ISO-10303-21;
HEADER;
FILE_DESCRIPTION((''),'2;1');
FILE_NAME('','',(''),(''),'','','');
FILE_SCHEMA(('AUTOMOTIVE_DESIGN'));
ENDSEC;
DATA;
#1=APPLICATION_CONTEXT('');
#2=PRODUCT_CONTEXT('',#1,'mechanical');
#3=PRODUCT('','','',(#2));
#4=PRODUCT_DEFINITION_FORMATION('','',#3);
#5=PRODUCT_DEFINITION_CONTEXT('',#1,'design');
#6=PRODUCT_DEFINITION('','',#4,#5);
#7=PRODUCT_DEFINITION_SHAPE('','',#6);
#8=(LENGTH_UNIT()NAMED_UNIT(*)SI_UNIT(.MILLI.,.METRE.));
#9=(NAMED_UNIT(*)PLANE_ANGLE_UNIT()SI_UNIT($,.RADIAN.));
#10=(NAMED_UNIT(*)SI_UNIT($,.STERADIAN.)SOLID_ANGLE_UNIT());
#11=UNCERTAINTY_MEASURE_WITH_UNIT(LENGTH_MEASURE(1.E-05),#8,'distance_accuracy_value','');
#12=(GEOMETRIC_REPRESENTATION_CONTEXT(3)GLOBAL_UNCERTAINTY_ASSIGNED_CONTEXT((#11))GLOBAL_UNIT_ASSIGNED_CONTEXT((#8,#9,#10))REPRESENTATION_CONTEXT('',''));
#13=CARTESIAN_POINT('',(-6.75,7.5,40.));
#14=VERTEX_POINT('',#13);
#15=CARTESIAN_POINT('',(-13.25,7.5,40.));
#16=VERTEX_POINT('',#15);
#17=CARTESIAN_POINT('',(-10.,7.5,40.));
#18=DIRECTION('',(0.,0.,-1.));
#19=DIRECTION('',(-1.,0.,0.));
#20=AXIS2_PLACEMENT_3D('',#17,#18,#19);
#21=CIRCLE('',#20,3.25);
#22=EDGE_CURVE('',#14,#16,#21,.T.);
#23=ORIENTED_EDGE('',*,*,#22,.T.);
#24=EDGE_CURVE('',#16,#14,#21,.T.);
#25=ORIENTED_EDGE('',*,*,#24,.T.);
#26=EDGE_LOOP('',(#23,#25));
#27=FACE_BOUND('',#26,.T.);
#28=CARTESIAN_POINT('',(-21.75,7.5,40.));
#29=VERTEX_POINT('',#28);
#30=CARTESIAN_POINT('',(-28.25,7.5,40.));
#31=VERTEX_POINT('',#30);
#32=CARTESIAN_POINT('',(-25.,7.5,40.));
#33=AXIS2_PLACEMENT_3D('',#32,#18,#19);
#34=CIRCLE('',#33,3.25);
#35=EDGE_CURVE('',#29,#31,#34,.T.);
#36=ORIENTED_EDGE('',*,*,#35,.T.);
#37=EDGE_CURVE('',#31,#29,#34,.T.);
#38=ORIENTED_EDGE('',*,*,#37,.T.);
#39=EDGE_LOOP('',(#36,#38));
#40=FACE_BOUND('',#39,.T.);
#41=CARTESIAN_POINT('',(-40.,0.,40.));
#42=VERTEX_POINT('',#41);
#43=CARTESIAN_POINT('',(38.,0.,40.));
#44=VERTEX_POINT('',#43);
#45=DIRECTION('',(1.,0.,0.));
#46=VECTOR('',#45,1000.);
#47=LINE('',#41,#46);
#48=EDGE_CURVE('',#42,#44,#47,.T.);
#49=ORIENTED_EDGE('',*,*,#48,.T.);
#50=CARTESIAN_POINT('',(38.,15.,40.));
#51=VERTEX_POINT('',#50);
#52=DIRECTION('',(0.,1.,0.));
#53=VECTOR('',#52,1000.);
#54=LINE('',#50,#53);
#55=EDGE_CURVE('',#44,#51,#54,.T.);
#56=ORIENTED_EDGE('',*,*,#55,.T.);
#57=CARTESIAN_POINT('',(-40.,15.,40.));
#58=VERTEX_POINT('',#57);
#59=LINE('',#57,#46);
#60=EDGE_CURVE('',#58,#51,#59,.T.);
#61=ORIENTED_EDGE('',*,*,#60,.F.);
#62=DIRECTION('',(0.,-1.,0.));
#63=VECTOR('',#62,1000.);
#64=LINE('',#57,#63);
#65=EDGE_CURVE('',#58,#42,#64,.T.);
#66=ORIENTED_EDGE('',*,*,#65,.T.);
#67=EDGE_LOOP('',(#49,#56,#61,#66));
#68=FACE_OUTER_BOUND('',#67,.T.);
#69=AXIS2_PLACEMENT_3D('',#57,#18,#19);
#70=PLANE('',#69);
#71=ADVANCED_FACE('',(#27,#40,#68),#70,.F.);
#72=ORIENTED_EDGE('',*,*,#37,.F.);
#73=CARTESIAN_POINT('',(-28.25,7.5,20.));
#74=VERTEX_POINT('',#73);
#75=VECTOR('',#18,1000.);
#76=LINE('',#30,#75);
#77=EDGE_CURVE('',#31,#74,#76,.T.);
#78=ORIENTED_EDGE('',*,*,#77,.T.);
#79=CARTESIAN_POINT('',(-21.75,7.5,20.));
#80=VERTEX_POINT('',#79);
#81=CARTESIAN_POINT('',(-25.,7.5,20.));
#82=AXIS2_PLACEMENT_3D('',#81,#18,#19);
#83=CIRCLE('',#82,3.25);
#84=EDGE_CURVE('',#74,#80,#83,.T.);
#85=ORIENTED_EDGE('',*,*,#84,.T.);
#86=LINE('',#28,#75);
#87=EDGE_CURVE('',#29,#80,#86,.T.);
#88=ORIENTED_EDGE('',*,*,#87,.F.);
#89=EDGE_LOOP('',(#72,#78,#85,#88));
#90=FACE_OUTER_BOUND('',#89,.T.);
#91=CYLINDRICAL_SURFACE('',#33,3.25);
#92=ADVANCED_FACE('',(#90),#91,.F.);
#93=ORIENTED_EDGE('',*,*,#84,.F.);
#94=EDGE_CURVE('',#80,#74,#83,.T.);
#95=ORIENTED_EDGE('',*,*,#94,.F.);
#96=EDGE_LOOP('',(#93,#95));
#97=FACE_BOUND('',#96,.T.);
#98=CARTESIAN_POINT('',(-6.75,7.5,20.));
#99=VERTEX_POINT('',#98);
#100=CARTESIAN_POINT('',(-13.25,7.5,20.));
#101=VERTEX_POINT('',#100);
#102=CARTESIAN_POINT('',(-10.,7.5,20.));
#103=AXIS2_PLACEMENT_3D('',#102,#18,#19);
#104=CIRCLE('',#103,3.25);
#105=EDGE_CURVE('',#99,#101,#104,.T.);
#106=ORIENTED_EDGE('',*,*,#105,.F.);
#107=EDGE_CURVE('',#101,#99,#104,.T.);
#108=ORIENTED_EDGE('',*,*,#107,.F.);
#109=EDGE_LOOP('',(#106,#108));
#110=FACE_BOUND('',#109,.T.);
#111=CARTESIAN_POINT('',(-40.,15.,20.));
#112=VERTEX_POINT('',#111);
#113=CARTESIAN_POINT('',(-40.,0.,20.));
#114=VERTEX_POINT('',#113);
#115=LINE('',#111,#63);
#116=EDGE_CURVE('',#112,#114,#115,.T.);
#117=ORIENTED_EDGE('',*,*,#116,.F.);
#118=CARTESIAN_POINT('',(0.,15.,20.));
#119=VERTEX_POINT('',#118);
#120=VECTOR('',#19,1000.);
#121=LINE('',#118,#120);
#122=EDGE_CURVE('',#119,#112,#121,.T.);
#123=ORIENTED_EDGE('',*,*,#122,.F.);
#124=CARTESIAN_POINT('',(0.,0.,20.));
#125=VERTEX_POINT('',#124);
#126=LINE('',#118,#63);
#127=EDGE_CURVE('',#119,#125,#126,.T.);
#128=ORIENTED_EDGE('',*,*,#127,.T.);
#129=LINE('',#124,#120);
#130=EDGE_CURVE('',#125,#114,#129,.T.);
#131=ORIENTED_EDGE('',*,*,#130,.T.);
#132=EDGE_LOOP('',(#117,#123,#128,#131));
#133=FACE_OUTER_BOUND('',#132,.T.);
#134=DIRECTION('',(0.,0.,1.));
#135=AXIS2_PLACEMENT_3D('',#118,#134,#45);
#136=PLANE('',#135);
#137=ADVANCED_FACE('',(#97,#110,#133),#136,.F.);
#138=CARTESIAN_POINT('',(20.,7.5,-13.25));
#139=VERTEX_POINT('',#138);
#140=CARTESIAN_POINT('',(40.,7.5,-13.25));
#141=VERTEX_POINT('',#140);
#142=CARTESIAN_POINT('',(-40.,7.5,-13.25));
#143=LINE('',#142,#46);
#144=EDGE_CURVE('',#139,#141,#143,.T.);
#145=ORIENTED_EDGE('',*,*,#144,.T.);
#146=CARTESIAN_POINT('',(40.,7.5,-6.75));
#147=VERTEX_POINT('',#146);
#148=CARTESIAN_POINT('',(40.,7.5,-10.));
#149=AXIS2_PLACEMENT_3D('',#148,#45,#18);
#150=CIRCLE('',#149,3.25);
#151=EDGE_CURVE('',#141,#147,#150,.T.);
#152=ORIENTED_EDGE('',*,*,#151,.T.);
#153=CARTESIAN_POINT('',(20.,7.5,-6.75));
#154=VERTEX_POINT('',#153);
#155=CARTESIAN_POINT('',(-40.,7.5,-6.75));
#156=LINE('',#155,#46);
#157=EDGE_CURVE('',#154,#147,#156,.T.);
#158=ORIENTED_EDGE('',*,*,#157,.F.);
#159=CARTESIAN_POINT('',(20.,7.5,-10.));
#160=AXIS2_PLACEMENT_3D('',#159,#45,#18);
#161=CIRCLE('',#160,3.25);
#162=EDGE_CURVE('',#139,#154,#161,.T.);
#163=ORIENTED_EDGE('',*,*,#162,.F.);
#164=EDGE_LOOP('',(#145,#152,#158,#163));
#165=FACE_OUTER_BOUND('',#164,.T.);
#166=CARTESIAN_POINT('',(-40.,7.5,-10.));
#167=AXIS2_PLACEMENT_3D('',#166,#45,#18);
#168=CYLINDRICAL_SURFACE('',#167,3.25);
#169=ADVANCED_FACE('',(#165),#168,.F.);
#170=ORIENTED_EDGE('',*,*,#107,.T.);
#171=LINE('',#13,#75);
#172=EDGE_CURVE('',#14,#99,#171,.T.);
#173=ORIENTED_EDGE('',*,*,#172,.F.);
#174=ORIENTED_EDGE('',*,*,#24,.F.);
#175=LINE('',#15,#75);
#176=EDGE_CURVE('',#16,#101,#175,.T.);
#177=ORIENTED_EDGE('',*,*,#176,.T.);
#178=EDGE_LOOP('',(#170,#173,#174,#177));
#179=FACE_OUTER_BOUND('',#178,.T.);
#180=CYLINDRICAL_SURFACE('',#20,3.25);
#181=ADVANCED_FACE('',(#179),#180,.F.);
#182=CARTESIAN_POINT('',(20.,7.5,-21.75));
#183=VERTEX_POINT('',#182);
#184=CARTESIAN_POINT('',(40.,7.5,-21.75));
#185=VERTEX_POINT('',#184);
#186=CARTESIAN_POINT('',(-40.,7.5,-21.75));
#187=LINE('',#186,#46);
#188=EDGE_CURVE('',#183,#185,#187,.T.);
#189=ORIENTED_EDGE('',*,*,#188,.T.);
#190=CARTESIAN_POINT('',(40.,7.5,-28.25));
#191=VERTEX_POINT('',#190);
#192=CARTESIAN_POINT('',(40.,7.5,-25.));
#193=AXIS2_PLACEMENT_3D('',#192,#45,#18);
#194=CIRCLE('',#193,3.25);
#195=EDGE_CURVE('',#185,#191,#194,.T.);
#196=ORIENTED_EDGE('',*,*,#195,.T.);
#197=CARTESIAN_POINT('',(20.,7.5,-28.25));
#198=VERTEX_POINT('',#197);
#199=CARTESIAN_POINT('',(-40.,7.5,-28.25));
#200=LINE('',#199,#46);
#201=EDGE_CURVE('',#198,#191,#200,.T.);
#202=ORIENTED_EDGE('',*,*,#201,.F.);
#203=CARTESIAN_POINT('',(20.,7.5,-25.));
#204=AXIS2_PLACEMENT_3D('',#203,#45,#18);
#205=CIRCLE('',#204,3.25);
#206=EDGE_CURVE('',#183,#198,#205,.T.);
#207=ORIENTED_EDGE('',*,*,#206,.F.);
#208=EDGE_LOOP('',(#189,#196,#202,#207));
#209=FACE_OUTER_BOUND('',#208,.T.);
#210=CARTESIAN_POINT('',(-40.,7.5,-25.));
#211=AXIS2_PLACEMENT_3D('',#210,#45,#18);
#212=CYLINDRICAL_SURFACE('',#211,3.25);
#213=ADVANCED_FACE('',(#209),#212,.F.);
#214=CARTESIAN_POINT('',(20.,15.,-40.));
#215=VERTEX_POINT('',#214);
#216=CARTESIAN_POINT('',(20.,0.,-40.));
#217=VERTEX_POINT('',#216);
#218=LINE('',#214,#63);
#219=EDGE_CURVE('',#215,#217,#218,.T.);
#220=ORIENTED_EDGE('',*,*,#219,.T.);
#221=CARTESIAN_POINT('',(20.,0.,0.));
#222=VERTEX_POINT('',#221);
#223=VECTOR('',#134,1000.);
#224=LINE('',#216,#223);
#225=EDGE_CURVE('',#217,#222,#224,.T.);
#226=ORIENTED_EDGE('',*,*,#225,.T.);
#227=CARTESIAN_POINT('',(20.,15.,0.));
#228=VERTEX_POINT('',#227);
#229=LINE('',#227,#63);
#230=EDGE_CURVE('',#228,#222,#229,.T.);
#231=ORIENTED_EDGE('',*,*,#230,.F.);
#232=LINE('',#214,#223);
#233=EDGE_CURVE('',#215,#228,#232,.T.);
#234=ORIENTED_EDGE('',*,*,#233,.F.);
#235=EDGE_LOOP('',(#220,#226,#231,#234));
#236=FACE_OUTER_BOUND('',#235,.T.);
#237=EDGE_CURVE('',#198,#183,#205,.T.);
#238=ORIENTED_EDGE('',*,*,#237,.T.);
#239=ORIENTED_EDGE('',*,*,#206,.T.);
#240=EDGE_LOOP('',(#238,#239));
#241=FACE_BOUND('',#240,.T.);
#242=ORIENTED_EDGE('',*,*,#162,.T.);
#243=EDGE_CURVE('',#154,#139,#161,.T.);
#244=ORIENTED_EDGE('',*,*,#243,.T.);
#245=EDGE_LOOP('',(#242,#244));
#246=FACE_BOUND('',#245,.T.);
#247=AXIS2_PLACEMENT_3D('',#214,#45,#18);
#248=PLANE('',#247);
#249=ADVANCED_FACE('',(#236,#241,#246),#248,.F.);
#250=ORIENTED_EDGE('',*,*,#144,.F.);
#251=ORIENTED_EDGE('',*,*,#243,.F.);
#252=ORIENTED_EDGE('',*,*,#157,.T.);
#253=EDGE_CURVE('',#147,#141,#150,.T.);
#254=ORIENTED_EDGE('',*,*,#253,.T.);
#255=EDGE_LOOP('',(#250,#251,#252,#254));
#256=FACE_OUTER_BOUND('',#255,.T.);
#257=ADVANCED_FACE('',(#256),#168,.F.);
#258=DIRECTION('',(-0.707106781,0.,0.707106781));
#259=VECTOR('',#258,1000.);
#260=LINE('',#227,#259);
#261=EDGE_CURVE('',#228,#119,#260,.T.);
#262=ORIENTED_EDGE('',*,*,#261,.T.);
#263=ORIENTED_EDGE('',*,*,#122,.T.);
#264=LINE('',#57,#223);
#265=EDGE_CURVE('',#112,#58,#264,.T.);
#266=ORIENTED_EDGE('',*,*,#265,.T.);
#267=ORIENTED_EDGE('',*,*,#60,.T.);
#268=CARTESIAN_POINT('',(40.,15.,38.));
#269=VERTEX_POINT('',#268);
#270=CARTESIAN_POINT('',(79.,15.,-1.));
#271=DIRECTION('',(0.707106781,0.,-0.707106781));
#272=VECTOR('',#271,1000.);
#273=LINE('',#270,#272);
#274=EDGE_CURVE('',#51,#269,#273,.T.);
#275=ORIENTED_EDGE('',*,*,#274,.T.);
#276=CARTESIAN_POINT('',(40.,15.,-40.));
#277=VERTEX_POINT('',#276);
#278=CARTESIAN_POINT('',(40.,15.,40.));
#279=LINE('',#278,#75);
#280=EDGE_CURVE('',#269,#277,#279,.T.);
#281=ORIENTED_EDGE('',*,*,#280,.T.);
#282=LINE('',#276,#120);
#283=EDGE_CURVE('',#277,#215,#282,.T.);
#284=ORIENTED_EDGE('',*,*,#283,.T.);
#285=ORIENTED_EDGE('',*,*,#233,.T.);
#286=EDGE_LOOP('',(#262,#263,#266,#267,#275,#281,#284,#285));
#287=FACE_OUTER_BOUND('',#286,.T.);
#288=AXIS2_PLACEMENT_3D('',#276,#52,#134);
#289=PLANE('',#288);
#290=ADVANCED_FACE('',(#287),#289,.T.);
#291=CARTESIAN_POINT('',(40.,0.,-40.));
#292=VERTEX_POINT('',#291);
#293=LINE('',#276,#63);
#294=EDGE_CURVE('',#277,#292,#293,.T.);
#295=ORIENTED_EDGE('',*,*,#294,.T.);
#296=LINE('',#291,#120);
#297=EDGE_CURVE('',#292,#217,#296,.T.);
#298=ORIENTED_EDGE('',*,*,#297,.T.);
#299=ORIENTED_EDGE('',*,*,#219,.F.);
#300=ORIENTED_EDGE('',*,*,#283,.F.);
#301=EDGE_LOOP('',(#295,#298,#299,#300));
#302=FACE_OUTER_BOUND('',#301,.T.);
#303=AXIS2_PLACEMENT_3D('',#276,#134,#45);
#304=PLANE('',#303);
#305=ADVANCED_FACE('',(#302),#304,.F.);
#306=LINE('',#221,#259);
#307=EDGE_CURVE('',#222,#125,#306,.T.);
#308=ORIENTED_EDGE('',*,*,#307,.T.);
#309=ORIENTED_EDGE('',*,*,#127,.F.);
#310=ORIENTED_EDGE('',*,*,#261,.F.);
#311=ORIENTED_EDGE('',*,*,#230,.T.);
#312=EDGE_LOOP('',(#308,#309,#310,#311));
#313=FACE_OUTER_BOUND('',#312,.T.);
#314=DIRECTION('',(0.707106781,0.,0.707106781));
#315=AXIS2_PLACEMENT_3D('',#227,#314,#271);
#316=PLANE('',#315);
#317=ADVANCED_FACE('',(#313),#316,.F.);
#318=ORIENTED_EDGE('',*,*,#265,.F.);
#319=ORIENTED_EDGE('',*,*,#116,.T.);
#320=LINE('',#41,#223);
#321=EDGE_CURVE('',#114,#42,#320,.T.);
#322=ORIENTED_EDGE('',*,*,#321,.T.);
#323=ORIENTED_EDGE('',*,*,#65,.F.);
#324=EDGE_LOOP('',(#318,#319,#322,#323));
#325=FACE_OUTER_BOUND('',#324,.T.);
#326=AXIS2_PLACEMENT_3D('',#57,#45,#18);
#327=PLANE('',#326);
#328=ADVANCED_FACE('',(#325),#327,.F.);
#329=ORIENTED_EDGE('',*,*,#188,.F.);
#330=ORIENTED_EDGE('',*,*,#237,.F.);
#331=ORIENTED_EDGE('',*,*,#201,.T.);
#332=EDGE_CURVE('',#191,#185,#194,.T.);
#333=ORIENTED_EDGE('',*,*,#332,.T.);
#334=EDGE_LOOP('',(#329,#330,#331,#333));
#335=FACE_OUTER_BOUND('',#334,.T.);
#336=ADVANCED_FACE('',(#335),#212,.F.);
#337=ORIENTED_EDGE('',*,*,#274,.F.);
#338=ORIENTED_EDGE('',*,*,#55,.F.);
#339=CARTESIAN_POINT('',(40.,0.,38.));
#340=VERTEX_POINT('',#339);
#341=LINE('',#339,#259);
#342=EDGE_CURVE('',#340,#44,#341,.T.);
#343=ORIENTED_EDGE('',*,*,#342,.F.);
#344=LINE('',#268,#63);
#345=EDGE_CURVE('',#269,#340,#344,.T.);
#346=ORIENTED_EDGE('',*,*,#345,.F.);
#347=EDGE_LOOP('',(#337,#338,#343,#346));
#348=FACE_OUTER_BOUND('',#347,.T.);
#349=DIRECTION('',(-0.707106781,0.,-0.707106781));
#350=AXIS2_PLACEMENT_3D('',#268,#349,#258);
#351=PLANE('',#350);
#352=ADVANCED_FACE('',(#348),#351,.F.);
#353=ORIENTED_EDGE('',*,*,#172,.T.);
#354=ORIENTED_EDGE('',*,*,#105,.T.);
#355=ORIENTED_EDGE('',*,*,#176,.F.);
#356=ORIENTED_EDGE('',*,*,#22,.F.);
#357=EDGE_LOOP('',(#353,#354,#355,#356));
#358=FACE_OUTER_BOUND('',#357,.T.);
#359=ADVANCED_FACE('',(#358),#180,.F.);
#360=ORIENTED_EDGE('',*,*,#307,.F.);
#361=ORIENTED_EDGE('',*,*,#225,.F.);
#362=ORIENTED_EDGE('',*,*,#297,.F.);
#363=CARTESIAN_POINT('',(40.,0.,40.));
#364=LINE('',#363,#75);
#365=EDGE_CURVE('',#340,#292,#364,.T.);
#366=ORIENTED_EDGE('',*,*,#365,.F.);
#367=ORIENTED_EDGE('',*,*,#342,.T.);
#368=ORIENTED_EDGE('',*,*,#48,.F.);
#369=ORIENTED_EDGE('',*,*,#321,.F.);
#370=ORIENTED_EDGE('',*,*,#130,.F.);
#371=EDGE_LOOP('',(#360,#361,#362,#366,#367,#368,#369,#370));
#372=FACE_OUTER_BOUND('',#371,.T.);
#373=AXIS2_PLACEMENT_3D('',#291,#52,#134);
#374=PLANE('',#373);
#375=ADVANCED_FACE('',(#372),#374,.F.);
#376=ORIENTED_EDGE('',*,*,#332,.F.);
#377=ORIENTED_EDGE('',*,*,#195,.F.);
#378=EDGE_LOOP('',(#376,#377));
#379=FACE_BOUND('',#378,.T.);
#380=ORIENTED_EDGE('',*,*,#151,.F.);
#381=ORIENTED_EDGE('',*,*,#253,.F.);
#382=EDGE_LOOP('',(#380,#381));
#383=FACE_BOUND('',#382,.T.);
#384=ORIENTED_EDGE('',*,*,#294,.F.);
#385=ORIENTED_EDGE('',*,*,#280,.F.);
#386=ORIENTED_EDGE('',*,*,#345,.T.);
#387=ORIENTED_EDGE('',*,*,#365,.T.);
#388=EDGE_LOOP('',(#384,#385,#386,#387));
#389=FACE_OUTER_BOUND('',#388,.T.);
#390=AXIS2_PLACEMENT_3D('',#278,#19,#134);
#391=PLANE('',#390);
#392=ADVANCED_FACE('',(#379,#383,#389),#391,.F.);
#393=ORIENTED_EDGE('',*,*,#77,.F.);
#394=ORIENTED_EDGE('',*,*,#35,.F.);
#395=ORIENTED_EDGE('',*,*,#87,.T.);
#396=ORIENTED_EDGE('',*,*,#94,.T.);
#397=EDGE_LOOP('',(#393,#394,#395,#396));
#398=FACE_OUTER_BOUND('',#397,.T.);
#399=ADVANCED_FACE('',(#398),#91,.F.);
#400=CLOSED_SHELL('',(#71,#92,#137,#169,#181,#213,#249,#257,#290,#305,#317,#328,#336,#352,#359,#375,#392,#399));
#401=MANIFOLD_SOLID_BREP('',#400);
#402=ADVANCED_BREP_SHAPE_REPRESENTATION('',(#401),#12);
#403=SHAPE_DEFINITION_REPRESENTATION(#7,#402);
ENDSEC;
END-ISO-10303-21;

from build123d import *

# Parameters (mm, degrees)
BOSS_EXTRUDE_1_DEPTH   = 15
SKETCH_4_R             = 3.25
CUT_EXTRUDE_1_DEPTH    = 74.654599313
LINEAR_PATTERN_1_COUNT = 2
LINEAR_PATTERN_1_PITCH = 15
SKETCH_5_R             = 3.25
CUT_EXTRUDE_2_DEPTH    = 91.691785736
LINEAR_PATTERN_2_COUNT = 2
LINEAR_PATTERN_2_PITCH = 15
CHAMFER_1_SIZE         = 2


with BuildPart() as part:
    # Sketch 3 → Boss-Extrude 1 (new body)
    with BuildSketch(Plane(origin=(0, 0, 0), x_dir=(1, 0, 0), z_dir=(0, 1, 0))):
        Polygon((40, 40), (20, 40), (20, 0), (0, -20), (-40, -20), (-40, -40), (40, -40), align=None)
    extrude(amount=BOSS_EXTRUDE_1_DEPTH)

    # Sketch 4 → Cut-Extrude 1 (cut, through all)
    with BuildSketch(Plane(origin=(0, 0, 20), x_dir=(-1, 0, 0), z_dir=(0, 0, -1))):
        with Locations((10, 7.5)):
            Circle(SKETCH_4_R)
    cut_extrude_1 = extrude(amount=-CUT_EXTRUDE_1_DEPTH, mode=Mode.SUBTRACT)

    # Linear Pattern 1: Cut-Extrude 1 ×2
    with Locations(*[(-i * LINEAR_PATTERN_1_PITCH, 0, 0) for i in range(1, LINEAR_PATTERN_1_COUNT)]):
        add(cut_extrude_1, mode=Mode.SUBTRACT)

    # Sketch 5 → Cut-Extrude 2 (cut, through all)
    with BuildSketch(Plane(origin=(40, 0, 0), x_dir=(0, 0, -1), z_dir=(1, 0, 0))):
        with Locations((10, 7.5)):
            Circle(SKETCH_5_R)
    cut_extrude_2 = extrude(amount=-CUT_EXTRUDE_2_DEPTH, mode=Mode.SUBTRACT)

    # Linear Pattern 2: Cut-Extrude 2 ×2
    with Locations(*[(0, 0, -i * LINEAR_PATTERN_2_PITCH) for i in range(1, LINEAR_PATTERN_2_COUNT)]):
        add(cut_extrude_2, mode=Mode.SUBTRACT)

    # Chamfer 1
    chamfer_1_edges = [part.edges().sort_by_distance(p)[0] for p in [
        (40, 7.5, 40),
    ]]
    chamfer(chamfer_1_edges, length=CHAMFER_1_SIZE)


solid = part.part
